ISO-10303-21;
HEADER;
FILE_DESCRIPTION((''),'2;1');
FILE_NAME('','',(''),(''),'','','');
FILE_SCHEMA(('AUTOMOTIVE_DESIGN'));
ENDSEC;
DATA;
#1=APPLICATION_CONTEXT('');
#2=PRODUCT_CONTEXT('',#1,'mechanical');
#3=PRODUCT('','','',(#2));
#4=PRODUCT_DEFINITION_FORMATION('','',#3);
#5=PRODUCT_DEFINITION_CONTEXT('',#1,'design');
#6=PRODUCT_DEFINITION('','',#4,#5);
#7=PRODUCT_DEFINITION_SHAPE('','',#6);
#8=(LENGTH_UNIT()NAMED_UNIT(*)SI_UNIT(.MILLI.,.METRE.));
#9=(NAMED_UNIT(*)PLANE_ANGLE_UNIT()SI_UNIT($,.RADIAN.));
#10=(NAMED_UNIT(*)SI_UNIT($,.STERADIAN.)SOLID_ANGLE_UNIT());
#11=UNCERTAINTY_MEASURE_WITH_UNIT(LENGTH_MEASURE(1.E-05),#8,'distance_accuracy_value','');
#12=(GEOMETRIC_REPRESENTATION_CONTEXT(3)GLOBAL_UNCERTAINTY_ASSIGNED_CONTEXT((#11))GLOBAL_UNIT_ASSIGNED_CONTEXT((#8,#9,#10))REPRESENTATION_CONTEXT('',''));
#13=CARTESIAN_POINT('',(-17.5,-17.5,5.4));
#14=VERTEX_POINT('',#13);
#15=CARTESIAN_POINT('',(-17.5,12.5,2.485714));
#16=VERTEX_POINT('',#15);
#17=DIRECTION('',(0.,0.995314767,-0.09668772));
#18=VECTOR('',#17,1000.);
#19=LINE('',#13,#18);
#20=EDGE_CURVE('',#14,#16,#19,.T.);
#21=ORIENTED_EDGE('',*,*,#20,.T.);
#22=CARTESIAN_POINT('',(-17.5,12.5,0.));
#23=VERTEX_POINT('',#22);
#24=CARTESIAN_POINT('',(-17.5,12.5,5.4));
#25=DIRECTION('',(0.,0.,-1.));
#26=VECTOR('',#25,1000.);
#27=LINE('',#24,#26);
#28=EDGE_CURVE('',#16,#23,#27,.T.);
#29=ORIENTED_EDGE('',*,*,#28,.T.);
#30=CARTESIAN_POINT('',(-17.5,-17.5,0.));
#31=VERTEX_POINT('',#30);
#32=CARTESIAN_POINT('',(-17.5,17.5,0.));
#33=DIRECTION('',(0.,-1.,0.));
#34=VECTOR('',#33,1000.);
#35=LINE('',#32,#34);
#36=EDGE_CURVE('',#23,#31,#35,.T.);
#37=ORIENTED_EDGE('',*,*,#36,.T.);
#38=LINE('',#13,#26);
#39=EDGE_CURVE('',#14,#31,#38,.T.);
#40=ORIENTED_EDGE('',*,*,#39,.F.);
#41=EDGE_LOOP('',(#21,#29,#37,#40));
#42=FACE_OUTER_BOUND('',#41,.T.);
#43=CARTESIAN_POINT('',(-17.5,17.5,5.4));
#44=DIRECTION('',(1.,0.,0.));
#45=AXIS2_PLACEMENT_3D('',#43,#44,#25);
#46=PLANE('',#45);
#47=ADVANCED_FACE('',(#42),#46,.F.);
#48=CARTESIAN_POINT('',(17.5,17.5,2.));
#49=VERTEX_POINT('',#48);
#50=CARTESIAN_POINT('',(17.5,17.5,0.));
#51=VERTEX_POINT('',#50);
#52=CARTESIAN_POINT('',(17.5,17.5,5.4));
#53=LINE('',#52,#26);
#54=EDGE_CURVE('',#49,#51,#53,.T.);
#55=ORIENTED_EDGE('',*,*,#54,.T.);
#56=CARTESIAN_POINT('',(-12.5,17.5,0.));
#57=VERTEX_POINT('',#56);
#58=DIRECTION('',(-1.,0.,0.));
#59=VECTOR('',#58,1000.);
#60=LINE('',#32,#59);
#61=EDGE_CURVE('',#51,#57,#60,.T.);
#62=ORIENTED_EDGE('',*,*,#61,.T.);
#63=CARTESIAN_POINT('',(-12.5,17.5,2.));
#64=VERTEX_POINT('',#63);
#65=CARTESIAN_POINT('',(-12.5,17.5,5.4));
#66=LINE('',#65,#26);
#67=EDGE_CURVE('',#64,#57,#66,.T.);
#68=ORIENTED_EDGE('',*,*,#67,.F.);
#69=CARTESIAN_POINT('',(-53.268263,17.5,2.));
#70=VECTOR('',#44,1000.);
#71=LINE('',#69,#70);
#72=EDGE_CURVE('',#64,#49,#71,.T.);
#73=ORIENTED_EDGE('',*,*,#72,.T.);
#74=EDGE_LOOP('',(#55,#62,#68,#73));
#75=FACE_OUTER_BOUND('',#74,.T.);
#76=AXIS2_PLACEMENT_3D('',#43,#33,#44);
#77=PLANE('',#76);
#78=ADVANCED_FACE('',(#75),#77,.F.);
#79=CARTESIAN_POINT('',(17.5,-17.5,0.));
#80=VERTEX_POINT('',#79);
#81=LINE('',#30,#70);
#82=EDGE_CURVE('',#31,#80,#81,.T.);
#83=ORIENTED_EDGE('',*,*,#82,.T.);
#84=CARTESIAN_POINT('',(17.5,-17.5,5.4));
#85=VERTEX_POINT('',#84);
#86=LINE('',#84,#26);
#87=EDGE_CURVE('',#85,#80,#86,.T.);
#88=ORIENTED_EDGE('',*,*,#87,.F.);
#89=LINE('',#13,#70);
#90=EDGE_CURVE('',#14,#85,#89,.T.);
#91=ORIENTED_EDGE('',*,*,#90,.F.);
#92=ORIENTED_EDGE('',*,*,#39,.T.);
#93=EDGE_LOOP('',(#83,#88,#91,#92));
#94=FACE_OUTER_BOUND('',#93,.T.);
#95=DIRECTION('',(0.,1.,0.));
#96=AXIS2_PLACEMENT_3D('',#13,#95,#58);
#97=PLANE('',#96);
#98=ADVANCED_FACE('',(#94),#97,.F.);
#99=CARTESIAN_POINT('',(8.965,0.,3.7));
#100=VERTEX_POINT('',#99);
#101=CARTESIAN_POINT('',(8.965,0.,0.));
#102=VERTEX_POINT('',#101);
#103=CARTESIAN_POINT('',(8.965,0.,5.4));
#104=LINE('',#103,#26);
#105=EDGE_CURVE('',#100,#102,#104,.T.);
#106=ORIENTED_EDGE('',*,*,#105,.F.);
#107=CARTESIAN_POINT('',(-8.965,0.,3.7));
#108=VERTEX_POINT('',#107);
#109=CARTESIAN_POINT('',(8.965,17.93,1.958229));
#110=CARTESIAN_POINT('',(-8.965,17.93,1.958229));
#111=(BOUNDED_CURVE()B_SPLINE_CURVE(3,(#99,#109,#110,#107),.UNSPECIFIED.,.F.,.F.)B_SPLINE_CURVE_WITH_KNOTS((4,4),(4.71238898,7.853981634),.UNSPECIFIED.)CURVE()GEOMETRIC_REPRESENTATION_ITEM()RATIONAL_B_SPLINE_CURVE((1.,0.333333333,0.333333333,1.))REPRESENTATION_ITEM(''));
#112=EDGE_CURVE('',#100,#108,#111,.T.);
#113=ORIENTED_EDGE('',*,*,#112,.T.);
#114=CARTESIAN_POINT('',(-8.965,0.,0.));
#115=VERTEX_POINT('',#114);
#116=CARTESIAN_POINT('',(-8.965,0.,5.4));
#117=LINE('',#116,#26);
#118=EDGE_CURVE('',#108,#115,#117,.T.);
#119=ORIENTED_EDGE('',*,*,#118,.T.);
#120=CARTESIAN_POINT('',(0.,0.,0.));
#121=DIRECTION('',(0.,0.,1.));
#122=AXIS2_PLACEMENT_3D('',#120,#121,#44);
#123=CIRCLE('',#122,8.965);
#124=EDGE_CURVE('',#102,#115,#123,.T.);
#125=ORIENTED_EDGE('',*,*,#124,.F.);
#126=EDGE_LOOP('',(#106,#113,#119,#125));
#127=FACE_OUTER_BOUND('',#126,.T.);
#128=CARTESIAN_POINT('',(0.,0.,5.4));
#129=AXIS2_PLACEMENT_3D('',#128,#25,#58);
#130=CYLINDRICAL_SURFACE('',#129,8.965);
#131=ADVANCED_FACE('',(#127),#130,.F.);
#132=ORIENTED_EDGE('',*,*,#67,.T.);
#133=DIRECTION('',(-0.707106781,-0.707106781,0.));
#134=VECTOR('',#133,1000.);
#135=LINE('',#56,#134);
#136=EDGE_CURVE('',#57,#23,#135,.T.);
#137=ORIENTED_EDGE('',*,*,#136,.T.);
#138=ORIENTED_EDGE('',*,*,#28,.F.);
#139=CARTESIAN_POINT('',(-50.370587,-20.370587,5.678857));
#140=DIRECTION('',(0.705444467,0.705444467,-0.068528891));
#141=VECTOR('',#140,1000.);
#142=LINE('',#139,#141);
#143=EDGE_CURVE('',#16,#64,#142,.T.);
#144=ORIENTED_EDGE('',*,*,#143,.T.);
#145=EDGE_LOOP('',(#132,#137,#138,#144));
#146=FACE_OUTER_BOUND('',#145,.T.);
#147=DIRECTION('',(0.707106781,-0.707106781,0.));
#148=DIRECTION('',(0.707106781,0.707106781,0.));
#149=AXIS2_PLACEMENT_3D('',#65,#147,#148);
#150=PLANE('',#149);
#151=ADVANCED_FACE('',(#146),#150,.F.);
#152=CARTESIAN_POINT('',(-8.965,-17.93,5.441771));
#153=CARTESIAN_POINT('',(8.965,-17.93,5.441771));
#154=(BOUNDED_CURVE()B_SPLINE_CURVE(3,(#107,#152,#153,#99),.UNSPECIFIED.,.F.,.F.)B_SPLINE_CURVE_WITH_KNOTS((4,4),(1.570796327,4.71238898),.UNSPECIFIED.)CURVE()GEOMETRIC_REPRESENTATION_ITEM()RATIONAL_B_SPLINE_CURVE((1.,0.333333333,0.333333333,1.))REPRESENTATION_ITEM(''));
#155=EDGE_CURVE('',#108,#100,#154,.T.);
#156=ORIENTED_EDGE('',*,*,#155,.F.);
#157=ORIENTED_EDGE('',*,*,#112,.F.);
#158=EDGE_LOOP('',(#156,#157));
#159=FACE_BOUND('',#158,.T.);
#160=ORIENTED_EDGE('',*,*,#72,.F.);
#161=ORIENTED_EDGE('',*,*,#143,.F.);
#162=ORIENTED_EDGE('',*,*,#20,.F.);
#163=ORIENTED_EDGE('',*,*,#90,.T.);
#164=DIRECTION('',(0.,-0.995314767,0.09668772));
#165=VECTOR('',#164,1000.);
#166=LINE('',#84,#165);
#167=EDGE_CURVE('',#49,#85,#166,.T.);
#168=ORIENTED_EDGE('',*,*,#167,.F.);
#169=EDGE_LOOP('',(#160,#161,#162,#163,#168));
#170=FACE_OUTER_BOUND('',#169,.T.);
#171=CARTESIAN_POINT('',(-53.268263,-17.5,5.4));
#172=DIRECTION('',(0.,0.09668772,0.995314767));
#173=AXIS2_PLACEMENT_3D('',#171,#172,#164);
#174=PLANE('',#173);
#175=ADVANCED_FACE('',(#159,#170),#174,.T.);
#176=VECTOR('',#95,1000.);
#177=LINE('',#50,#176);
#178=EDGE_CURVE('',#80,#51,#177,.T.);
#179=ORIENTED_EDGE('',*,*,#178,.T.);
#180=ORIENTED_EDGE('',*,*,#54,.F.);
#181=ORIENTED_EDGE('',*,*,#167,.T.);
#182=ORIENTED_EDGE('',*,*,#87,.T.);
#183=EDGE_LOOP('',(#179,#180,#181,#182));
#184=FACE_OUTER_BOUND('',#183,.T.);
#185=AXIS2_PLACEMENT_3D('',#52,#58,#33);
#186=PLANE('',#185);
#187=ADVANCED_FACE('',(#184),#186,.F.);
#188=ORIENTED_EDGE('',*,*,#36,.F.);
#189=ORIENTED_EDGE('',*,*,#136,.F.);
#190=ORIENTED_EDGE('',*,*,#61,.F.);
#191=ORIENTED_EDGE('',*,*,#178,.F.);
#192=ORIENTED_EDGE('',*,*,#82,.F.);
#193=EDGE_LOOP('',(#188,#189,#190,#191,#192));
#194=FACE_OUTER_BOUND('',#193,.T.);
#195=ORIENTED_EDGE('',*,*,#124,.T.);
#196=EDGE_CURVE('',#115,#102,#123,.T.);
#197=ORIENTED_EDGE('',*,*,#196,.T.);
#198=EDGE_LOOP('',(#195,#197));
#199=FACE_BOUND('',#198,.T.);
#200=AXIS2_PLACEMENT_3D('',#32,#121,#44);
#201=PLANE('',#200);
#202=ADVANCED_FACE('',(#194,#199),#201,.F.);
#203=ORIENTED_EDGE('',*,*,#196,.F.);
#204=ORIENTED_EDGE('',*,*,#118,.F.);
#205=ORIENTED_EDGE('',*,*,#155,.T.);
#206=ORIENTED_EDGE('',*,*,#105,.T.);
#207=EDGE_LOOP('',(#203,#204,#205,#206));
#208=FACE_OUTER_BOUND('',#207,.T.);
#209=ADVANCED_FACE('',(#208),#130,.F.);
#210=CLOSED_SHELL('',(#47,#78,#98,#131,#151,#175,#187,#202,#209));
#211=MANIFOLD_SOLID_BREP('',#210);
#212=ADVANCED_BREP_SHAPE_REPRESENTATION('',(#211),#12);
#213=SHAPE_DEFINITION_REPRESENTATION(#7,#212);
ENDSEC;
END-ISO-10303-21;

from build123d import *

# Parameters (mm, degrees)
SKETCH1_W          = 35
SKETCH1_H          = 35
SKETCH1_R          = 8.965
BOSS_EXTRUDE_DEPTH = 5.4
SKETCH2_OUTSIDE_W  = 17.358
SKETCH2_OUTSIDE_H  = 46.958
CUT_EXTRUDE1_DEPTH = 35
CUT_EXTRUDE2_DEPTH = 26.331008665


with BuildPart() as part:
    # Sketch1 → Boss-Extrude (new body)
    with BuildSketch(Plane.XY):
        Rectangle(SKETCH1_W, SKETCH1_H)
        with Locations(Location((0, 0, 0), (0, 0, 180))):
            Circle(SKETCH1_R, mode=Mode.SUBTRACT)
    extrude(amount=BOSS_EXTRUDE_DEPTH)

    # Sketch2 outside → Cut-Extrude1 (cut)
    with BuildSketch(Plane(origin=(17.5, 0, 0), x_dir=(0, 0, -1), z_dir=(1, 0, 0))):
        with Locations((-2.7, 0)):
            Rectangle(SKETCH2_OUTSIDE_W, SKETCH2_OUTSIDE_H)
        Polygon((-5.4, -17.5), (-2, 17.5), (0, 17.5), (0, -17.5), align=None, mode=Mode.SUBTRACT)
    extrude(amount=-CUT_EXTRUDE1_DEPTH, mode=Mode.SUBTRACT)

    # Sketch3 → Cut-Extrude2 (cut, through all)
    with BuildSketch(Plane(origin=(0, 0, 0), x_dir=(-1, 0, 0), z_dir=(0, 0, -1))):
        Polygon((12.5, 17.5), (17.5, 12.5), (17.5, 17.5), align=None)
    extrude(amount=-CUT_EXTRUDE2_DEPTH, mode=Mode.SUBTRACT)


solid = part.part
